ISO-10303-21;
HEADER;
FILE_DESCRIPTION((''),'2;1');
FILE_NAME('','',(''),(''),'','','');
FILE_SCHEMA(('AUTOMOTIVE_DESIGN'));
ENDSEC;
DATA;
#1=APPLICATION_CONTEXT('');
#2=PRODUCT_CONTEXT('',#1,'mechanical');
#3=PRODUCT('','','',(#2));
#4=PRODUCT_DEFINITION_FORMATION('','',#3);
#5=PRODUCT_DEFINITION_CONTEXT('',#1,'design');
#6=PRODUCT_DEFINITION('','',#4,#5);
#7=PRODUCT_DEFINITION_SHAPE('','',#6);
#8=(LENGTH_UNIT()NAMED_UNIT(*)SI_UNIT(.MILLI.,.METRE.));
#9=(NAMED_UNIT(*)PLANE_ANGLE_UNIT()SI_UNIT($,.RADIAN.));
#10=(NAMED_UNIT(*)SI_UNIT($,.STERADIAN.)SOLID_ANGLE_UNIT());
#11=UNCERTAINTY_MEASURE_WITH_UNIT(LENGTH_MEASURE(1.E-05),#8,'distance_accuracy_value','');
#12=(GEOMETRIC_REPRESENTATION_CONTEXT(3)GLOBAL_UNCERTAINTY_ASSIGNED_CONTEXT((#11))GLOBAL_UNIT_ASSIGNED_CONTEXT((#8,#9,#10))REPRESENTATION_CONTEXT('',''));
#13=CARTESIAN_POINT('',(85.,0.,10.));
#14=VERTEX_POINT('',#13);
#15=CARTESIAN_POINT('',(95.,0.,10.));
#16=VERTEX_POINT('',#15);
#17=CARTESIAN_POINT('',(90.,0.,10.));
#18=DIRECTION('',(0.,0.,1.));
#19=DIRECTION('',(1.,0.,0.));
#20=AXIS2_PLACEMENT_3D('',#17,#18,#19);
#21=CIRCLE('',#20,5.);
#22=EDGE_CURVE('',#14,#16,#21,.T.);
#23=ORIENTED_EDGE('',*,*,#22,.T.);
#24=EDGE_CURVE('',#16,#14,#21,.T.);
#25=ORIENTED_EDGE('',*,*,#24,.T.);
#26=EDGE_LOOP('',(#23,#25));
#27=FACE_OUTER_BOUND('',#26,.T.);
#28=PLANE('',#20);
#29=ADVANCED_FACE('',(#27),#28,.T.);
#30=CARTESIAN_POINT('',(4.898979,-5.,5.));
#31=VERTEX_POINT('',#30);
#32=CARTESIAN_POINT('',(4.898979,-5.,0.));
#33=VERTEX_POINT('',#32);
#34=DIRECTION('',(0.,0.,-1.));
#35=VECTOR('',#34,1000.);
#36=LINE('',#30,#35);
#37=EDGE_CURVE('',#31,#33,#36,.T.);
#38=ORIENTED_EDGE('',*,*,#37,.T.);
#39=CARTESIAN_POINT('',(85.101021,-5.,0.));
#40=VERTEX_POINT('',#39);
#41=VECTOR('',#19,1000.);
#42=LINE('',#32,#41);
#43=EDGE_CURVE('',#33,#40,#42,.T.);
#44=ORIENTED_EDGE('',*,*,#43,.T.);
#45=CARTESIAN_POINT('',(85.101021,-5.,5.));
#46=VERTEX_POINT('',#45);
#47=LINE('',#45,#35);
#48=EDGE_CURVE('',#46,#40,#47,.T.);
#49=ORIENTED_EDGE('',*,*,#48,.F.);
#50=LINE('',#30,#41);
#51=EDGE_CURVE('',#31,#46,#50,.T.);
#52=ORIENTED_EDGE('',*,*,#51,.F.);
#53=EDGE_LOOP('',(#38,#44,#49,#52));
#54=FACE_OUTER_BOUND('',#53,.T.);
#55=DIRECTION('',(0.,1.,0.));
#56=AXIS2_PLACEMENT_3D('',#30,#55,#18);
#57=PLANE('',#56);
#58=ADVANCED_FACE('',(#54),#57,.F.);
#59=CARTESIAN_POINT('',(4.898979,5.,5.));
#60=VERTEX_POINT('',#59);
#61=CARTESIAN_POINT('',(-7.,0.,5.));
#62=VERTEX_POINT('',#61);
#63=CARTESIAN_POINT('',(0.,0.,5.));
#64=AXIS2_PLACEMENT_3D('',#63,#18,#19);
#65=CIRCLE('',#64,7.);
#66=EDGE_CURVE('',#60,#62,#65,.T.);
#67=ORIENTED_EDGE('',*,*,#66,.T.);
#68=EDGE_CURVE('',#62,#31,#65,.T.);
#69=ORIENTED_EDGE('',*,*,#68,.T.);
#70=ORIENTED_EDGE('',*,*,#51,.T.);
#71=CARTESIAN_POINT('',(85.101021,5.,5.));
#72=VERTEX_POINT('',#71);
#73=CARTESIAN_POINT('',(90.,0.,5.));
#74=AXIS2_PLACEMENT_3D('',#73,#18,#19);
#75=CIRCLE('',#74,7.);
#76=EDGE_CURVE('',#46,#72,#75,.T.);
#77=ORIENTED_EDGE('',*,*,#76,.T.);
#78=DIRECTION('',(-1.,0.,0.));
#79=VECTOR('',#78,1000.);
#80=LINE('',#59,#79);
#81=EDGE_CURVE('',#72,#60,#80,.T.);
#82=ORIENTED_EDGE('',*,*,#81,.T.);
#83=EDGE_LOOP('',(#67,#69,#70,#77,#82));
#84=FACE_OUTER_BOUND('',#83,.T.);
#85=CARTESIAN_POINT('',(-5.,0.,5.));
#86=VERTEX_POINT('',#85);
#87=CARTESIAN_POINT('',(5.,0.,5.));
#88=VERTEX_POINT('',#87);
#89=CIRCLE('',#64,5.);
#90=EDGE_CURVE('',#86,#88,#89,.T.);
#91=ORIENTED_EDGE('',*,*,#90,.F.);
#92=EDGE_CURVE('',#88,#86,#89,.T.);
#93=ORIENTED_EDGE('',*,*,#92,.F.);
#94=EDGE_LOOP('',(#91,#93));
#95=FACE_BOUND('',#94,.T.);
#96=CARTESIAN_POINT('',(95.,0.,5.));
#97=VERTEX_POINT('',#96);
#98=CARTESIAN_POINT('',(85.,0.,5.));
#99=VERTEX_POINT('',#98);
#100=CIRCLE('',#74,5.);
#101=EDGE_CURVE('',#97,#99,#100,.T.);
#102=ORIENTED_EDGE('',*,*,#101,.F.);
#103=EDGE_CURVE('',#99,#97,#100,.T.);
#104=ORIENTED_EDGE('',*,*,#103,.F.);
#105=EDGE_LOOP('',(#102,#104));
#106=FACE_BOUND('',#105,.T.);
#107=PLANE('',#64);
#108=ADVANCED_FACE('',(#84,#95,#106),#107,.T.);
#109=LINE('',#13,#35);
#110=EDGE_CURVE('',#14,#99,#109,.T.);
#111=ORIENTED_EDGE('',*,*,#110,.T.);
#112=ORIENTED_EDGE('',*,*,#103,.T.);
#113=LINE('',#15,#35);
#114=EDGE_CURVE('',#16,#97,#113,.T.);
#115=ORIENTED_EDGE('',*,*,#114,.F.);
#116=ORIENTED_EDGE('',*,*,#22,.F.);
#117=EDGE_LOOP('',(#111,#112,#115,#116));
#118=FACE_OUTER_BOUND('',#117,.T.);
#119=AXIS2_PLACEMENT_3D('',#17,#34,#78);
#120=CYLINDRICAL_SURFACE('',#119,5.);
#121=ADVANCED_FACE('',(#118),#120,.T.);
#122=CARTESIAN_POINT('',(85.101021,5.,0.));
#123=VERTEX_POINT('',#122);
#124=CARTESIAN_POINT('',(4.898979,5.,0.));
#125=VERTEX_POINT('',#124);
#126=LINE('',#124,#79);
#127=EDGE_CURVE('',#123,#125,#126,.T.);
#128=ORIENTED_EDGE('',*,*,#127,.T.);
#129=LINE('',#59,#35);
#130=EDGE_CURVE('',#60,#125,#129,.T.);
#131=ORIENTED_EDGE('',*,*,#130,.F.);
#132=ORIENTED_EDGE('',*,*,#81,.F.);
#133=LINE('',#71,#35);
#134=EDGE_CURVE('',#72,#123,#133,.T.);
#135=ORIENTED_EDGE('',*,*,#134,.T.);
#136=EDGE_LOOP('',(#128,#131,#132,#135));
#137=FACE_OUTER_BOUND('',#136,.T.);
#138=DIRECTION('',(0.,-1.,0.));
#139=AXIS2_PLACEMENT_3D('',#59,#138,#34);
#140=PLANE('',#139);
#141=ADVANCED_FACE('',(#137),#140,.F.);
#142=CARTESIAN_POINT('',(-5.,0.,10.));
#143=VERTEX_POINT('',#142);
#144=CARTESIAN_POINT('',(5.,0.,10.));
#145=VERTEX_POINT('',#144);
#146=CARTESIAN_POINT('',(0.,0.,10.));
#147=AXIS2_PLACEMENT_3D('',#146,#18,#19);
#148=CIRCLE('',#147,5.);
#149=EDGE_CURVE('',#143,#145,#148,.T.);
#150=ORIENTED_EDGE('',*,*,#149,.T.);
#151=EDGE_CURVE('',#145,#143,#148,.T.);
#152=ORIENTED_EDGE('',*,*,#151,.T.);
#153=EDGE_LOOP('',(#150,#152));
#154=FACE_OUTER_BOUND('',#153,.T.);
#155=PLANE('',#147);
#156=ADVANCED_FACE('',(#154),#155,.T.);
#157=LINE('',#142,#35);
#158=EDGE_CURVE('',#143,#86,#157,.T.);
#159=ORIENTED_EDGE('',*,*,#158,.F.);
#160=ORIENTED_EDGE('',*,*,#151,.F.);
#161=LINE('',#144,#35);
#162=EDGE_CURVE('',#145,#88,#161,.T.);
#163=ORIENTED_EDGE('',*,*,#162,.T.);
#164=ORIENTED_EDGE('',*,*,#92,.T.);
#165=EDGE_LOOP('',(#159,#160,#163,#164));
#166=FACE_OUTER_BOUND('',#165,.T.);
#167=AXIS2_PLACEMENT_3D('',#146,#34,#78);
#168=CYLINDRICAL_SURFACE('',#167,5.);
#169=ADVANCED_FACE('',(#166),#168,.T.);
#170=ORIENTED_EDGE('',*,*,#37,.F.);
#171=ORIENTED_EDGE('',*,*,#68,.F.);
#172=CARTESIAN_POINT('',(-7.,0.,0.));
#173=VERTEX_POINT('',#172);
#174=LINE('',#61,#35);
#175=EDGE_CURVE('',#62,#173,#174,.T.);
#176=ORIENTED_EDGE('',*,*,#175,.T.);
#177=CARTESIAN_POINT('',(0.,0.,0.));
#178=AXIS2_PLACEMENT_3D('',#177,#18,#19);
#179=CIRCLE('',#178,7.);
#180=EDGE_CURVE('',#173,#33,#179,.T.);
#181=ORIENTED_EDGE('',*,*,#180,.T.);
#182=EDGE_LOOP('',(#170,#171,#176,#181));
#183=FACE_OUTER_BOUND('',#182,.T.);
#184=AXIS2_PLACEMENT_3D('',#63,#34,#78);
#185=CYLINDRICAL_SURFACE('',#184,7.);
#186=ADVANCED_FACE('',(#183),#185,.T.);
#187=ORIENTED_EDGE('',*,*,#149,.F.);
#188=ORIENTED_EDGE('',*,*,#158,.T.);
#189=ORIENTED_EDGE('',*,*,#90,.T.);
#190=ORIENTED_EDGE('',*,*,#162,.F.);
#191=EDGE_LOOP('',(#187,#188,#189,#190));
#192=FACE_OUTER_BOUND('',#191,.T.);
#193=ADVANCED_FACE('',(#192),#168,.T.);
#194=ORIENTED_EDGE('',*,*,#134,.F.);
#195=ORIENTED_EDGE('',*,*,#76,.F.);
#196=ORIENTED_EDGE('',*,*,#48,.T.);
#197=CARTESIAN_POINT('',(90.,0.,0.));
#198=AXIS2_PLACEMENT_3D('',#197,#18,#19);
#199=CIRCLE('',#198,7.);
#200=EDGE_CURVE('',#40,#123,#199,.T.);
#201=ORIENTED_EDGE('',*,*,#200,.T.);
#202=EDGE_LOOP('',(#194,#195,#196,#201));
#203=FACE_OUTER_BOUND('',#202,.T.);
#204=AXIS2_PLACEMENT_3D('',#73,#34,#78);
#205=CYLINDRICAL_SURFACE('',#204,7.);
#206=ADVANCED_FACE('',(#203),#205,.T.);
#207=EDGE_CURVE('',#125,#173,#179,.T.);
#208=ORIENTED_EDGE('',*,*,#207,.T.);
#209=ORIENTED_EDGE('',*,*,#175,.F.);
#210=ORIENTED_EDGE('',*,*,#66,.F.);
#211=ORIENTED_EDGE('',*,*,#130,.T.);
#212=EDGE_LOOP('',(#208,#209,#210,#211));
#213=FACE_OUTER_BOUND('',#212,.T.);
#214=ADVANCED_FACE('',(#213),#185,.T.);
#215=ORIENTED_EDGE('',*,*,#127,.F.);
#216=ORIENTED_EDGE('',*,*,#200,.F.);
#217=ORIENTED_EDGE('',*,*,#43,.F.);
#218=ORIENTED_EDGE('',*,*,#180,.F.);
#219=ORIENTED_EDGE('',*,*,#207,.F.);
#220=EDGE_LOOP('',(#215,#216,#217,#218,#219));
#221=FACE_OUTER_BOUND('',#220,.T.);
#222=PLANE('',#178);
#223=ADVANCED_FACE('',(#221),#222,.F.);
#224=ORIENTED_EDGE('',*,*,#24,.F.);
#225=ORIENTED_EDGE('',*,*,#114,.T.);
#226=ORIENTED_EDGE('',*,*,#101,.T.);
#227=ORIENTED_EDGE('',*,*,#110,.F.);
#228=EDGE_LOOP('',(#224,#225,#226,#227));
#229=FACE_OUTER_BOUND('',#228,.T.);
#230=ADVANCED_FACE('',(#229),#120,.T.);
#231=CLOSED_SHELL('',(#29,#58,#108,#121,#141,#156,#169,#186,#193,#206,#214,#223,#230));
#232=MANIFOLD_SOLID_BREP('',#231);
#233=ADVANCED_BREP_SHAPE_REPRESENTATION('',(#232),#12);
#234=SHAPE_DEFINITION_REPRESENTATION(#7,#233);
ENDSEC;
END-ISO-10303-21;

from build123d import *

# Parameters (mm, degrees)
BASE_EXTRUDE_DEPTH  = 5
SKETCH2_R           = 5
BOSS_EXTRUDE1_DEPTH = 5


with BuildPart() as part:
    # Sketch1 → Base-Extrude (new body)
    with BuildSketch(Plane.XY):
        with BuildLine():
            Line((4.898979486, -5), (85.101020514, -5))
            ThreePointArc((85.101020514, -5), (97, 0), (85.101020514, 5))
            Line((85.101020514, 5), (4.898979486, 5))
            ThreePointArc((4.898979486, 5), (-7, 0), (4.898979486, -5))
        make_face()
    extrude(amount=BASE_EXTRUDE_DEPTH)

    # Sketch2 → Boss-Extrude1 (add)
    with BuildSketch(Plane.XY.offset(5)):
        Circle(SKETCH2_R)
        with Locations((90, 0)):
            Circle(SKETCH2_R)
    extrude(amount=BOSS_EXTRUDE1_DEPTH)


solid = part.part
